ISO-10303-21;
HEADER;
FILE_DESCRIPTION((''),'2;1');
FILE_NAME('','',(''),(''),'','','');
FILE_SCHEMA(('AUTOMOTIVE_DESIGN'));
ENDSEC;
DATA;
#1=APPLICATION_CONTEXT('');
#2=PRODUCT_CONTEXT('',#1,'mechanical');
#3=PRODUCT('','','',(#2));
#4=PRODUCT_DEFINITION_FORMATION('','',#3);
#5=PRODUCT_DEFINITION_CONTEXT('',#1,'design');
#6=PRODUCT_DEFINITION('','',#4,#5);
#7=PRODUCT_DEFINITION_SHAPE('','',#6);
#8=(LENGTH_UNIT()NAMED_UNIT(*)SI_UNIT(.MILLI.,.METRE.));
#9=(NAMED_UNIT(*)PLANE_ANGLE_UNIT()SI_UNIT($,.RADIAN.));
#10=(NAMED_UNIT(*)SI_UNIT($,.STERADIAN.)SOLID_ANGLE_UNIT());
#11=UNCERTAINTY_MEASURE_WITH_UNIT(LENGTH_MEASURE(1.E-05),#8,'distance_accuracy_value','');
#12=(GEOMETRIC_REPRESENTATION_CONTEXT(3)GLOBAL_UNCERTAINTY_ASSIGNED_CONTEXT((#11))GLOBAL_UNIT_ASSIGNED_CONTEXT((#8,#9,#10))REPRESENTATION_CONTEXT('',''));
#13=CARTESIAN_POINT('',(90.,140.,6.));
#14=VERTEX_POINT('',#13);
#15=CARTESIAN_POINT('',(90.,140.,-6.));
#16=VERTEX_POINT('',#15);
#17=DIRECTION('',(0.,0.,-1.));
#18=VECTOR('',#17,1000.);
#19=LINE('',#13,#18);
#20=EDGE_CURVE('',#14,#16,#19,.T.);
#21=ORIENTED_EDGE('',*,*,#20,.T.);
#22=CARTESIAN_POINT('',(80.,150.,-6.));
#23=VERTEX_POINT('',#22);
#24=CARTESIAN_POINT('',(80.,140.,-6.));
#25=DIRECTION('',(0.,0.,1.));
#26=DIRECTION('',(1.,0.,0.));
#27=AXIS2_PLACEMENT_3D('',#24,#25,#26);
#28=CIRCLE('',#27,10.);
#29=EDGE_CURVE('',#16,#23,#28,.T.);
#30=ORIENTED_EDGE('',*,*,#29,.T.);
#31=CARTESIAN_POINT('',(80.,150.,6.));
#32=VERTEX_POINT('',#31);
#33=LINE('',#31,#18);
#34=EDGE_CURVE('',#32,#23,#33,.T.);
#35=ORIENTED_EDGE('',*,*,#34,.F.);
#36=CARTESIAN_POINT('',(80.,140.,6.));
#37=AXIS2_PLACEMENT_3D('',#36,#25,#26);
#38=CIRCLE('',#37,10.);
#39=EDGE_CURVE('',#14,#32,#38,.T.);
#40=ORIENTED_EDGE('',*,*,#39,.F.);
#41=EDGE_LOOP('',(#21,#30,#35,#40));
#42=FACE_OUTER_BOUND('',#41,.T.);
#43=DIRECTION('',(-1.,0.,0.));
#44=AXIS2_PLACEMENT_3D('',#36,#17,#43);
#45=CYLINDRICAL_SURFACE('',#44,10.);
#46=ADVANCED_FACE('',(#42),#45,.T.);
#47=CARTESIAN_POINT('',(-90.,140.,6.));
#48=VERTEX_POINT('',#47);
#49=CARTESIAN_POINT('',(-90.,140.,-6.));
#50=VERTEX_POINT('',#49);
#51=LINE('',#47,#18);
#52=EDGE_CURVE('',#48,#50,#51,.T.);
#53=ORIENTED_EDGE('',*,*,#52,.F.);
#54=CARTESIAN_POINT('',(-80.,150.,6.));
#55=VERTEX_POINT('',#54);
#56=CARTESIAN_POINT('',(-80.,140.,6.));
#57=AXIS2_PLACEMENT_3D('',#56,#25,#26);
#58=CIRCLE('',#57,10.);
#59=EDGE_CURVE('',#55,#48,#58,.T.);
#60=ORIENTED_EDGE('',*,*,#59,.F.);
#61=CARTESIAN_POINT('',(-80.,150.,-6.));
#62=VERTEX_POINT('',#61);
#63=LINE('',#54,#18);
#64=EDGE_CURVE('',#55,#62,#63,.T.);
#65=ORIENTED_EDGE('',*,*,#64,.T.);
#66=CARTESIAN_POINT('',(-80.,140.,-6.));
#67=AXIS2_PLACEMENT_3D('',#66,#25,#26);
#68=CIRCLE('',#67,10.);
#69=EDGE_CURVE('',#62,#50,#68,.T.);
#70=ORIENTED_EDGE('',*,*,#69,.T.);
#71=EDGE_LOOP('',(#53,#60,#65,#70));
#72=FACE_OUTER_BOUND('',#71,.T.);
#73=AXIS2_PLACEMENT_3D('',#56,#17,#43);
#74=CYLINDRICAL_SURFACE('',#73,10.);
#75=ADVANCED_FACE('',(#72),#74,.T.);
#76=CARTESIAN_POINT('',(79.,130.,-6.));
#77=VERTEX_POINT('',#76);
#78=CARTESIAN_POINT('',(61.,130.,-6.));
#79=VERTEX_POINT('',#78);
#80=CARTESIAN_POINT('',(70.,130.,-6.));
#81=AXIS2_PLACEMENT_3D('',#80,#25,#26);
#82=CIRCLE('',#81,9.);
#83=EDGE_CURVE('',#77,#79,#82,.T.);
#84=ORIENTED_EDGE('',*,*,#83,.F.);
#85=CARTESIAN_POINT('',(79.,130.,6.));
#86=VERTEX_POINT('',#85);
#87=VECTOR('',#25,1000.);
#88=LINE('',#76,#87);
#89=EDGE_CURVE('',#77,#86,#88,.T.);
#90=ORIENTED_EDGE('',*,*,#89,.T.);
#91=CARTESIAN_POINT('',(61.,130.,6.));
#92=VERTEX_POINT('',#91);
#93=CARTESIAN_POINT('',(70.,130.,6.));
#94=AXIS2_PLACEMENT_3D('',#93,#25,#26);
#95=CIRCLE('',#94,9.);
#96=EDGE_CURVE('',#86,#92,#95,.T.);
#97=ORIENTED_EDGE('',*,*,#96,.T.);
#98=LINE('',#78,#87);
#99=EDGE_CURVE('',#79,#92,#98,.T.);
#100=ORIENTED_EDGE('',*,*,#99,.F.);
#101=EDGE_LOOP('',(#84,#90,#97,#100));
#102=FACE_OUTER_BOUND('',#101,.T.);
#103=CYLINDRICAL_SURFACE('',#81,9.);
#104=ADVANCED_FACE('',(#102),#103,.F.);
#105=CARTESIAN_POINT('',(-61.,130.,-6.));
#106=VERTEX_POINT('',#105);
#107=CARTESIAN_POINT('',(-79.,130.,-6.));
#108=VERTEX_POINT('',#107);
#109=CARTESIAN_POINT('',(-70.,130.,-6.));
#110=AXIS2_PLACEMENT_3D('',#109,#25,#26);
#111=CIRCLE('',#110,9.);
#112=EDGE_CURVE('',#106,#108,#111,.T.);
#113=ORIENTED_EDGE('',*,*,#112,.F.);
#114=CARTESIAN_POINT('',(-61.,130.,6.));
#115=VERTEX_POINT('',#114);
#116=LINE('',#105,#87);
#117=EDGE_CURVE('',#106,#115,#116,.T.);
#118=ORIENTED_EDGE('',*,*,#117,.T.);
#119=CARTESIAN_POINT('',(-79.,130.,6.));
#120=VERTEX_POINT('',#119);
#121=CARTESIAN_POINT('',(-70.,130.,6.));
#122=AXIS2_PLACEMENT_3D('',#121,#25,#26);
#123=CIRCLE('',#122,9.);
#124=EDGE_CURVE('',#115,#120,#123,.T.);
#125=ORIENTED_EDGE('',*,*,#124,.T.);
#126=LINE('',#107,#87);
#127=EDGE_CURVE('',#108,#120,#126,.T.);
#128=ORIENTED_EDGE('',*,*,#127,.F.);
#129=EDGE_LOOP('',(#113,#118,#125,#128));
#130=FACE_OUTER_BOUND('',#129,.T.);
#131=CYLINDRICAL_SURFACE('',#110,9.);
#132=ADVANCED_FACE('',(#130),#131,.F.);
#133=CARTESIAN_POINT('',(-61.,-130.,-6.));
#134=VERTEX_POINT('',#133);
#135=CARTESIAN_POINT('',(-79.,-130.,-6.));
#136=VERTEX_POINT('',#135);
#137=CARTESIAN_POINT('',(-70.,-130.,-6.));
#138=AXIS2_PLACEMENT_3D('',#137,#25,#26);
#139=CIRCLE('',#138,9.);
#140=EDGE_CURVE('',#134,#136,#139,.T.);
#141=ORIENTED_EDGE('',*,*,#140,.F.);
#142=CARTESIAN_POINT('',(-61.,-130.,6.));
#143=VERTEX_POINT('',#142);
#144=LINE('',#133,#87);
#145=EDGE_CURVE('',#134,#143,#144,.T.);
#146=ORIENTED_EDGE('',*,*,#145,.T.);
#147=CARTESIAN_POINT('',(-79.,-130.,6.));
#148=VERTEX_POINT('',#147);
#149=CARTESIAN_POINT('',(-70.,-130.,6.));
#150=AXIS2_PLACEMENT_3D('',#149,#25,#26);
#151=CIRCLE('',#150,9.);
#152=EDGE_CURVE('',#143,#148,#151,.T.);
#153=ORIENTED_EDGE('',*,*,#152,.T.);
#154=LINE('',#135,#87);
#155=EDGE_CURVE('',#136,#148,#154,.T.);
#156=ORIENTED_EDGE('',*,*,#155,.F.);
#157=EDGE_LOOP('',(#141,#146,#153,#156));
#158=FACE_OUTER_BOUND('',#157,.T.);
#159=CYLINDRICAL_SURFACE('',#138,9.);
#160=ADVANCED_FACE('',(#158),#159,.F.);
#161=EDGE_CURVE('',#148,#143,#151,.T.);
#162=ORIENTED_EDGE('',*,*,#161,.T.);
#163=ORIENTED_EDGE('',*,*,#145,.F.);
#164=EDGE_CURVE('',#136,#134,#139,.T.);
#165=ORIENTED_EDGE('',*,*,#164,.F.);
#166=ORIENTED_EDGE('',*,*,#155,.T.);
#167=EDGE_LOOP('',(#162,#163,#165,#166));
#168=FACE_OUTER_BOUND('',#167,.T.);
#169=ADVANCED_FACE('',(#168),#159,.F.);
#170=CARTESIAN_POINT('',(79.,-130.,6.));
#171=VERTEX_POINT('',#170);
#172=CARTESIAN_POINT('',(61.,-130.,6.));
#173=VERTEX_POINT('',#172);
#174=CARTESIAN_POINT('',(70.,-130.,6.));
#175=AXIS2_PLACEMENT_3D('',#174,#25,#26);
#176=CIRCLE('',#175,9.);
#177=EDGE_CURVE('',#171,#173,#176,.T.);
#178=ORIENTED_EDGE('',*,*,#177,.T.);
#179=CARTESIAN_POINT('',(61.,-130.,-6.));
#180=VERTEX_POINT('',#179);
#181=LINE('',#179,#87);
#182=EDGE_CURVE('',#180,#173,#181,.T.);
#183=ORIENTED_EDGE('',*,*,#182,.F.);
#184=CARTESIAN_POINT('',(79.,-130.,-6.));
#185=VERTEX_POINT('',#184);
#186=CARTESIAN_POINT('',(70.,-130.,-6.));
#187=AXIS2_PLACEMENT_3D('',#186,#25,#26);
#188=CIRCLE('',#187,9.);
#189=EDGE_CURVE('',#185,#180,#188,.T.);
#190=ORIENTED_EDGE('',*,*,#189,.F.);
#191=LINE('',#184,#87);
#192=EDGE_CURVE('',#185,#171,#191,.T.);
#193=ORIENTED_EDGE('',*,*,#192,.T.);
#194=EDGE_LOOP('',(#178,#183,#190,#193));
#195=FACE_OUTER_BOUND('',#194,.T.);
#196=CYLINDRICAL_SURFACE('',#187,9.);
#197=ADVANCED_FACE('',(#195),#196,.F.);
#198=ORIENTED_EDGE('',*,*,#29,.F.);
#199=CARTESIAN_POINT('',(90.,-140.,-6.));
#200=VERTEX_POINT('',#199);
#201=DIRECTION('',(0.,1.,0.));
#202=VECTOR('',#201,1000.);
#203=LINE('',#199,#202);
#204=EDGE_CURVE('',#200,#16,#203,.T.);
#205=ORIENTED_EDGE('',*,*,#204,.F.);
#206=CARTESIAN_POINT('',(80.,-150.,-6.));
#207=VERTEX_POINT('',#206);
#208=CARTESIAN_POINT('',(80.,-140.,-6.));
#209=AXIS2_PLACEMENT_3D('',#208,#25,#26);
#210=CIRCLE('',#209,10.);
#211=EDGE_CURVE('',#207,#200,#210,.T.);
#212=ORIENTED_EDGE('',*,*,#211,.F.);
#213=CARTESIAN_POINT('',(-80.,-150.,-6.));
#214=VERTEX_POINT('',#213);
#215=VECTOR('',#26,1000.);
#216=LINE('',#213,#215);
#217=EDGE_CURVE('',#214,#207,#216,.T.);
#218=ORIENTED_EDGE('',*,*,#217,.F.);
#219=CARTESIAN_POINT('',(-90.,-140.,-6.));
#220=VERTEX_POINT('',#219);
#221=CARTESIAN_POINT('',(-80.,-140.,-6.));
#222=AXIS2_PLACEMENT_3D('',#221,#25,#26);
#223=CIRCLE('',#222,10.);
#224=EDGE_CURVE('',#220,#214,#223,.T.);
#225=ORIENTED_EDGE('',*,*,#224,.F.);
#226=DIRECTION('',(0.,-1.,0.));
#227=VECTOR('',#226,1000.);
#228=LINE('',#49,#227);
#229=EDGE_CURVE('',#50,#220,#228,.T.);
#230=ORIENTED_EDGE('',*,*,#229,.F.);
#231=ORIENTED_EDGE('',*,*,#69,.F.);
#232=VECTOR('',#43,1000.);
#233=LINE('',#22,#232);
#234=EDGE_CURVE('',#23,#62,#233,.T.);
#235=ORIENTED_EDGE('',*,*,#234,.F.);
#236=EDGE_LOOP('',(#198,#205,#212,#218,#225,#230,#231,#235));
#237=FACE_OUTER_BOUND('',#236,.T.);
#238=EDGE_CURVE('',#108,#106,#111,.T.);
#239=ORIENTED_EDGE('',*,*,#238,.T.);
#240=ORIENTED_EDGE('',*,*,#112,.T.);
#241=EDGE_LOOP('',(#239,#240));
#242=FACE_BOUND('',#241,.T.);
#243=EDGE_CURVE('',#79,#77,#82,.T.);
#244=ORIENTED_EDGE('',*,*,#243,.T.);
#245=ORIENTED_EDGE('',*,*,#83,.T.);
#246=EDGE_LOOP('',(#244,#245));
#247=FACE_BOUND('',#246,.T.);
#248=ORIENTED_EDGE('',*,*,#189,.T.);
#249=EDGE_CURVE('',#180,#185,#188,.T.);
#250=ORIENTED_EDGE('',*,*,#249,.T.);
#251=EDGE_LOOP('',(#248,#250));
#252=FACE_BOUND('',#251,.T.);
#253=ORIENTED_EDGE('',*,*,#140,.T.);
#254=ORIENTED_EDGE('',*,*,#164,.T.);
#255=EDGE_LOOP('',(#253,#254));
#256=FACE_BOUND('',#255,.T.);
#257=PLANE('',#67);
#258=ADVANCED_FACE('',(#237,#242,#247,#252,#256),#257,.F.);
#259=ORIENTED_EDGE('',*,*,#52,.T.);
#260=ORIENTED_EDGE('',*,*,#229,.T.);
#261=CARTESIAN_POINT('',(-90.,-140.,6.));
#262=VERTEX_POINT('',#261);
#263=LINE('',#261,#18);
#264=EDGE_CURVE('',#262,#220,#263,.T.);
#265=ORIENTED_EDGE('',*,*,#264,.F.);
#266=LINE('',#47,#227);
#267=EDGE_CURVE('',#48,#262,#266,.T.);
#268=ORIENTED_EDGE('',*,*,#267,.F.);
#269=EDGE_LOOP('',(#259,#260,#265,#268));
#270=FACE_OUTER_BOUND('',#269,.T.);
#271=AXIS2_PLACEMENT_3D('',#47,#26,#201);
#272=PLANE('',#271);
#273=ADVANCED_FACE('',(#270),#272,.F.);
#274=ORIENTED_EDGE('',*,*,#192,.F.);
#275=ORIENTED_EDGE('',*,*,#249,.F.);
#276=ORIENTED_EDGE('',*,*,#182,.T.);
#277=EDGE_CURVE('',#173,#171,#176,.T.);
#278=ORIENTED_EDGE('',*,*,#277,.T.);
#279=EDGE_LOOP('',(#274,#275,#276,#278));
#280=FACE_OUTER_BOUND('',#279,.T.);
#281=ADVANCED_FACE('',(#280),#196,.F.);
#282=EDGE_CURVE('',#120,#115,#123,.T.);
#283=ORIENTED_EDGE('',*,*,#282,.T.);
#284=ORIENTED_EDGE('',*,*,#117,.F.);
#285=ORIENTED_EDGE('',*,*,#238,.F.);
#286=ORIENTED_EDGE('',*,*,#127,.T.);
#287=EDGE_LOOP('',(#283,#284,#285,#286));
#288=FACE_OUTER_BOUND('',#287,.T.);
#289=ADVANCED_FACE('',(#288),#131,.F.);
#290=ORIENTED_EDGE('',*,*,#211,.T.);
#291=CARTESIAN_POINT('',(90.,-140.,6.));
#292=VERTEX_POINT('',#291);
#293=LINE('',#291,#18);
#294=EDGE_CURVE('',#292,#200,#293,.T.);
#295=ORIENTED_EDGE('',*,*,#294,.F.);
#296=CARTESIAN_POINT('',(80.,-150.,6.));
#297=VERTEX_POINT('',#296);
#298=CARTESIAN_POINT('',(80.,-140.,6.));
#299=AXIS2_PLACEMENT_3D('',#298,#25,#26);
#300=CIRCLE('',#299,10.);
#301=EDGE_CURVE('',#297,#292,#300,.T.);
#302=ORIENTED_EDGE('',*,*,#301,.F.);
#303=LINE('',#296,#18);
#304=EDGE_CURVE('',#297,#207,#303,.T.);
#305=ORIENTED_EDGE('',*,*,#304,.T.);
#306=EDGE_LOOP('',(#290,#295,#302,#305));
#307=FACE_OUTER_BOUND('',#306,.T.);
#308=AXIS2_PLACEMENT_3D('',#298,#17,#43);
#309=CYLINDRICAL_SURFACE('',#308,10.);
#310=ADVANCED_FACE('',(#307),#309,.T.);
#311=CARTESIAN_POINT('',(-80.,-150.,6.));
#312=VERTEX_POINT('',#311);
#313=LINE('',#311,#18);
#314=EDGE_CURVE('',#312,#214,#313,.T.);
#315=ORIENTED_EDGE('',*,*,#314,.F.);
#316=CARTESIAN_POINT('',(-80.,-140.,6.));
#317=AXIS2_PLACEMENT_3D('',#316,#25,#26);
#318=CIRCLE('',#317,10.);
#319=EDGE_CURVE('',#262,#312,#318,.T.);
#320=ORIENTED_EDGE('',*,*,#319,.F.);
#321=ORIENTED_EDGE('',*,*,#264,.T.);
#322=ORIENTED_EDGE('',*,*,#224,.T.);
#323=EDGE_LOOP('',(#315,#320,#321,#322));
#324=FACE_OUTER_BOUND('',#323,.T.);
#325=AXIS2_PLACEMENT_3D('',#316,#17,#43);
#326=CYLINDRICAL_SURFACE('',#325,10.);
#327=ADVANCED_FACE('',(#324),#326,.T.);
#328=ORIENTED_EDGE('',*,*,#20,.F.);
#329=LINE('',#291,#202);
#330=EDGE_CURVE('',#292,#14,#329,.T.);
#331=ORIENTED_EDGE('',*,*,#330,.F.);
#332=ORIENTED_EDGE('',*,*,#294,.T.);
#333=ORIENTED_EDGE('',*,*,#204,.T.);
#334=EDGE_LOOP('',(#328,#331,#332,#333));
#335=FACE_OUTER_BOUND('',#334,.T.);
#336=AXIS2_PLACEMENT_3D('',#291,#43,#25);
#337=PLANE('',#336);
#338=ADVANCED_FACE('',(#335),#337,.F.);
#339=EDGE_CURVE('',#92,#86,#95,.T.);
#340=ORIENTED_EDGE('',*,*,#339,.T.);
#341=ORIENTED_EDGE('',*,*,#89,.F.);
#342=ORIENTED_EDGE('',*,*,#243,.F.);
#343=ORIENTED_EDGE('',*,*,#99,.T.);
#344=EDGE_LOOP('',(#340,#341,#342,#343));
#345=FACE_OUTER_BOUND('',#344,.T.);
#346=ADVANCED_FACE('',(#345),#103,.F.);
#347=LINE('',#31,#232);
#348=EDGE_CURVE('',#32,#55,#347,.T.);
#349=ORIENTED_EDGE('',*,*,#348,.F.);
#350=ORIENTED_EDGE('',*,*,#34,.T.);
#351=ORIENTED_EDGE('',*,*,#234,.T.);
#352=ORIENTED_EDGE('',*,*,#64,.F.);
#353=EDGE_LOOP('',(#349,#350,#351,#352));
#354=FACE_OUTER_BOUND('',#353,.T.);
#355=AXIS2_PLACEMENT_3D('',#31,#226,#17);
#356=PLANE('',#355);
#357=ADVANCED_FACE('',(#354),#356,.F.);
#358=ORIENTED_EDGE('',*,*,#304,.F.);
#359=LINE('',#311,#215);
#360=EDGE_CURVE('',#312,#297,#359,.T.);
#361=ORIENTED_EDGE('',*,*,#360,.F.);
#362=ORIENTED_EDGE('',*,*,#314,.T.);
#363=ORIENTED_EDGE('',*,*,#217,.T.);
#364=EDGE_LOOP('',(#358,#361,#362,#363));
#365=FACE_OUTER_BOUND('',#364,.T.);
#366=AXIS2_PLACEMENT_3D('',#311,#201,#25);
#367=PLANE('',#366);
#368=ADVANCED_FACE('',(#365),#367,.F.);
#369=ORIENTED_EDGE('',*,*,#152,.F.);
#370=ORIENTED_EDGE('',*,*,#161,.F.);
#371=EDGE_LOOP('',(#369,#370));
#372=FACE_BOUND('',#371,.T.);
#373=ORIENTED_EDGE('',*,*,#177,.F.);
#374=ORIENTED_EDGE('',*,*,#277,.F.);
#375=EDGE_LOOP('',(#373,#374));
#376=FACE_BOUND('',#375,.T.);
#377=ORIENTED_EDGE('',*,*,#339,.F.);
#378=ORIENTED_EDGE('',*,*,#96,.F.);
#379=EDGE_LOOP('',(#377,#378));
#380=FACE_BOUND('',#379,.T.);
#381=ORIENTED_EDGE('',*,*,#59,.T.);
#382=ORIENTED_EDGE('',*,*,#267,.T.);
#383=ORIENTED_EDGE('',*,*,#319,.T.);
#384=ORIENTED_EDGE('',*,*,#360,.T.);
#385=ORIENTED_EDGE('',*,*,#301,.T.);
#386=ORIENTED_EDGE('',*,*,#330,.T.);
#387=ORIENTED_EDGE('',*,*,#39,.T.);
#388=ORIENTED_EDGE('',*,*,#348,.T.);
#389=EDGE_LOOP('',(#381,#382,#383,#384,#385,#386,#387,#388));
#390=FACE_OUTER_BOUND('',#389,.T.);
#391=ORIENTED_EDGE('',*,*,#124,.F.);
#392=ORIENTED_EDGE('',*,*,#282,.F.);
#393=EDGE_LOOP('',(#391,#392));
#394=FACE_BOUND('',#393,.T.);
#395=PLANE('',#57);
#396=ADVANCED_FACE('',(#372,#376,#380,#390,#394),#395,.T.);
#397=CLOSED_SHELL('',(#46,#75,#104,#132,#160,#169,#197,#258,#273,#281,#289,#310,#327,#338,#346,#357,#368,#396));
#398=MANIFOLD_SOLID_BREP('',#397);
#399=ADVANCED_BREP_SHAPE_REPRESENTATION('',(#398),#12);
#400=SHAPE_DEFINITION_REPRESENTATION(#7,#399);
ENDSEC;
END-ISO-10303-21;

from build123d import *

# Parameters (mm, degrees)
EXTRUDE1_DEPTH = 6
SKETCH2_R      = 9
EXTRUDE2_DEPTH = 176.339670354


with BuildPart() as part:
    # Sketch1 → Extrude1 (new, symmetric)
    with BuildSketch(Plane.XY):
        with BuildLine():
            Line((80, 150), (-80, 150))
            ThreePointArc((-80, 150), (-87.071067812, 147.071067812), (-90, 140))
            Line((-90, 140), (-90, -140))
            ThreePointArc((-90, -140), (-87.071067812, -147.071067812), (-80, -150))
            Line((-80, -150), (80, -150))
            ThreePointArc((80, -150), (87.071067812, -147.071067812), (90, -140))
            Line((90, -140), (90, 140))
            ThreePointArc((90, 140), (87.071067812, 147.071067812), (80, 150))
        make_face()
    extrude(amount=EXTRUDE1_DEPTH, both=True)

    # Sketch2 → Extrude2 (cut, through all)
    with BuildSketch(Plane.XY.offset(6)):
        with Locations((-70, -130)):
            Circle(SKETCH2_R)
        with Locations((70, -130)):
            Circle(SKETCH2_R)
        with Locations((-70, 130)):
            Circle(SKETCH2_R)
        with Locations((70, 130)):
            Circle(SKETCH2_R)
    extrude(amount=-EXTRUDE2_DEPTH, mode=Mode.SUBTRACT)


solid = part.part
